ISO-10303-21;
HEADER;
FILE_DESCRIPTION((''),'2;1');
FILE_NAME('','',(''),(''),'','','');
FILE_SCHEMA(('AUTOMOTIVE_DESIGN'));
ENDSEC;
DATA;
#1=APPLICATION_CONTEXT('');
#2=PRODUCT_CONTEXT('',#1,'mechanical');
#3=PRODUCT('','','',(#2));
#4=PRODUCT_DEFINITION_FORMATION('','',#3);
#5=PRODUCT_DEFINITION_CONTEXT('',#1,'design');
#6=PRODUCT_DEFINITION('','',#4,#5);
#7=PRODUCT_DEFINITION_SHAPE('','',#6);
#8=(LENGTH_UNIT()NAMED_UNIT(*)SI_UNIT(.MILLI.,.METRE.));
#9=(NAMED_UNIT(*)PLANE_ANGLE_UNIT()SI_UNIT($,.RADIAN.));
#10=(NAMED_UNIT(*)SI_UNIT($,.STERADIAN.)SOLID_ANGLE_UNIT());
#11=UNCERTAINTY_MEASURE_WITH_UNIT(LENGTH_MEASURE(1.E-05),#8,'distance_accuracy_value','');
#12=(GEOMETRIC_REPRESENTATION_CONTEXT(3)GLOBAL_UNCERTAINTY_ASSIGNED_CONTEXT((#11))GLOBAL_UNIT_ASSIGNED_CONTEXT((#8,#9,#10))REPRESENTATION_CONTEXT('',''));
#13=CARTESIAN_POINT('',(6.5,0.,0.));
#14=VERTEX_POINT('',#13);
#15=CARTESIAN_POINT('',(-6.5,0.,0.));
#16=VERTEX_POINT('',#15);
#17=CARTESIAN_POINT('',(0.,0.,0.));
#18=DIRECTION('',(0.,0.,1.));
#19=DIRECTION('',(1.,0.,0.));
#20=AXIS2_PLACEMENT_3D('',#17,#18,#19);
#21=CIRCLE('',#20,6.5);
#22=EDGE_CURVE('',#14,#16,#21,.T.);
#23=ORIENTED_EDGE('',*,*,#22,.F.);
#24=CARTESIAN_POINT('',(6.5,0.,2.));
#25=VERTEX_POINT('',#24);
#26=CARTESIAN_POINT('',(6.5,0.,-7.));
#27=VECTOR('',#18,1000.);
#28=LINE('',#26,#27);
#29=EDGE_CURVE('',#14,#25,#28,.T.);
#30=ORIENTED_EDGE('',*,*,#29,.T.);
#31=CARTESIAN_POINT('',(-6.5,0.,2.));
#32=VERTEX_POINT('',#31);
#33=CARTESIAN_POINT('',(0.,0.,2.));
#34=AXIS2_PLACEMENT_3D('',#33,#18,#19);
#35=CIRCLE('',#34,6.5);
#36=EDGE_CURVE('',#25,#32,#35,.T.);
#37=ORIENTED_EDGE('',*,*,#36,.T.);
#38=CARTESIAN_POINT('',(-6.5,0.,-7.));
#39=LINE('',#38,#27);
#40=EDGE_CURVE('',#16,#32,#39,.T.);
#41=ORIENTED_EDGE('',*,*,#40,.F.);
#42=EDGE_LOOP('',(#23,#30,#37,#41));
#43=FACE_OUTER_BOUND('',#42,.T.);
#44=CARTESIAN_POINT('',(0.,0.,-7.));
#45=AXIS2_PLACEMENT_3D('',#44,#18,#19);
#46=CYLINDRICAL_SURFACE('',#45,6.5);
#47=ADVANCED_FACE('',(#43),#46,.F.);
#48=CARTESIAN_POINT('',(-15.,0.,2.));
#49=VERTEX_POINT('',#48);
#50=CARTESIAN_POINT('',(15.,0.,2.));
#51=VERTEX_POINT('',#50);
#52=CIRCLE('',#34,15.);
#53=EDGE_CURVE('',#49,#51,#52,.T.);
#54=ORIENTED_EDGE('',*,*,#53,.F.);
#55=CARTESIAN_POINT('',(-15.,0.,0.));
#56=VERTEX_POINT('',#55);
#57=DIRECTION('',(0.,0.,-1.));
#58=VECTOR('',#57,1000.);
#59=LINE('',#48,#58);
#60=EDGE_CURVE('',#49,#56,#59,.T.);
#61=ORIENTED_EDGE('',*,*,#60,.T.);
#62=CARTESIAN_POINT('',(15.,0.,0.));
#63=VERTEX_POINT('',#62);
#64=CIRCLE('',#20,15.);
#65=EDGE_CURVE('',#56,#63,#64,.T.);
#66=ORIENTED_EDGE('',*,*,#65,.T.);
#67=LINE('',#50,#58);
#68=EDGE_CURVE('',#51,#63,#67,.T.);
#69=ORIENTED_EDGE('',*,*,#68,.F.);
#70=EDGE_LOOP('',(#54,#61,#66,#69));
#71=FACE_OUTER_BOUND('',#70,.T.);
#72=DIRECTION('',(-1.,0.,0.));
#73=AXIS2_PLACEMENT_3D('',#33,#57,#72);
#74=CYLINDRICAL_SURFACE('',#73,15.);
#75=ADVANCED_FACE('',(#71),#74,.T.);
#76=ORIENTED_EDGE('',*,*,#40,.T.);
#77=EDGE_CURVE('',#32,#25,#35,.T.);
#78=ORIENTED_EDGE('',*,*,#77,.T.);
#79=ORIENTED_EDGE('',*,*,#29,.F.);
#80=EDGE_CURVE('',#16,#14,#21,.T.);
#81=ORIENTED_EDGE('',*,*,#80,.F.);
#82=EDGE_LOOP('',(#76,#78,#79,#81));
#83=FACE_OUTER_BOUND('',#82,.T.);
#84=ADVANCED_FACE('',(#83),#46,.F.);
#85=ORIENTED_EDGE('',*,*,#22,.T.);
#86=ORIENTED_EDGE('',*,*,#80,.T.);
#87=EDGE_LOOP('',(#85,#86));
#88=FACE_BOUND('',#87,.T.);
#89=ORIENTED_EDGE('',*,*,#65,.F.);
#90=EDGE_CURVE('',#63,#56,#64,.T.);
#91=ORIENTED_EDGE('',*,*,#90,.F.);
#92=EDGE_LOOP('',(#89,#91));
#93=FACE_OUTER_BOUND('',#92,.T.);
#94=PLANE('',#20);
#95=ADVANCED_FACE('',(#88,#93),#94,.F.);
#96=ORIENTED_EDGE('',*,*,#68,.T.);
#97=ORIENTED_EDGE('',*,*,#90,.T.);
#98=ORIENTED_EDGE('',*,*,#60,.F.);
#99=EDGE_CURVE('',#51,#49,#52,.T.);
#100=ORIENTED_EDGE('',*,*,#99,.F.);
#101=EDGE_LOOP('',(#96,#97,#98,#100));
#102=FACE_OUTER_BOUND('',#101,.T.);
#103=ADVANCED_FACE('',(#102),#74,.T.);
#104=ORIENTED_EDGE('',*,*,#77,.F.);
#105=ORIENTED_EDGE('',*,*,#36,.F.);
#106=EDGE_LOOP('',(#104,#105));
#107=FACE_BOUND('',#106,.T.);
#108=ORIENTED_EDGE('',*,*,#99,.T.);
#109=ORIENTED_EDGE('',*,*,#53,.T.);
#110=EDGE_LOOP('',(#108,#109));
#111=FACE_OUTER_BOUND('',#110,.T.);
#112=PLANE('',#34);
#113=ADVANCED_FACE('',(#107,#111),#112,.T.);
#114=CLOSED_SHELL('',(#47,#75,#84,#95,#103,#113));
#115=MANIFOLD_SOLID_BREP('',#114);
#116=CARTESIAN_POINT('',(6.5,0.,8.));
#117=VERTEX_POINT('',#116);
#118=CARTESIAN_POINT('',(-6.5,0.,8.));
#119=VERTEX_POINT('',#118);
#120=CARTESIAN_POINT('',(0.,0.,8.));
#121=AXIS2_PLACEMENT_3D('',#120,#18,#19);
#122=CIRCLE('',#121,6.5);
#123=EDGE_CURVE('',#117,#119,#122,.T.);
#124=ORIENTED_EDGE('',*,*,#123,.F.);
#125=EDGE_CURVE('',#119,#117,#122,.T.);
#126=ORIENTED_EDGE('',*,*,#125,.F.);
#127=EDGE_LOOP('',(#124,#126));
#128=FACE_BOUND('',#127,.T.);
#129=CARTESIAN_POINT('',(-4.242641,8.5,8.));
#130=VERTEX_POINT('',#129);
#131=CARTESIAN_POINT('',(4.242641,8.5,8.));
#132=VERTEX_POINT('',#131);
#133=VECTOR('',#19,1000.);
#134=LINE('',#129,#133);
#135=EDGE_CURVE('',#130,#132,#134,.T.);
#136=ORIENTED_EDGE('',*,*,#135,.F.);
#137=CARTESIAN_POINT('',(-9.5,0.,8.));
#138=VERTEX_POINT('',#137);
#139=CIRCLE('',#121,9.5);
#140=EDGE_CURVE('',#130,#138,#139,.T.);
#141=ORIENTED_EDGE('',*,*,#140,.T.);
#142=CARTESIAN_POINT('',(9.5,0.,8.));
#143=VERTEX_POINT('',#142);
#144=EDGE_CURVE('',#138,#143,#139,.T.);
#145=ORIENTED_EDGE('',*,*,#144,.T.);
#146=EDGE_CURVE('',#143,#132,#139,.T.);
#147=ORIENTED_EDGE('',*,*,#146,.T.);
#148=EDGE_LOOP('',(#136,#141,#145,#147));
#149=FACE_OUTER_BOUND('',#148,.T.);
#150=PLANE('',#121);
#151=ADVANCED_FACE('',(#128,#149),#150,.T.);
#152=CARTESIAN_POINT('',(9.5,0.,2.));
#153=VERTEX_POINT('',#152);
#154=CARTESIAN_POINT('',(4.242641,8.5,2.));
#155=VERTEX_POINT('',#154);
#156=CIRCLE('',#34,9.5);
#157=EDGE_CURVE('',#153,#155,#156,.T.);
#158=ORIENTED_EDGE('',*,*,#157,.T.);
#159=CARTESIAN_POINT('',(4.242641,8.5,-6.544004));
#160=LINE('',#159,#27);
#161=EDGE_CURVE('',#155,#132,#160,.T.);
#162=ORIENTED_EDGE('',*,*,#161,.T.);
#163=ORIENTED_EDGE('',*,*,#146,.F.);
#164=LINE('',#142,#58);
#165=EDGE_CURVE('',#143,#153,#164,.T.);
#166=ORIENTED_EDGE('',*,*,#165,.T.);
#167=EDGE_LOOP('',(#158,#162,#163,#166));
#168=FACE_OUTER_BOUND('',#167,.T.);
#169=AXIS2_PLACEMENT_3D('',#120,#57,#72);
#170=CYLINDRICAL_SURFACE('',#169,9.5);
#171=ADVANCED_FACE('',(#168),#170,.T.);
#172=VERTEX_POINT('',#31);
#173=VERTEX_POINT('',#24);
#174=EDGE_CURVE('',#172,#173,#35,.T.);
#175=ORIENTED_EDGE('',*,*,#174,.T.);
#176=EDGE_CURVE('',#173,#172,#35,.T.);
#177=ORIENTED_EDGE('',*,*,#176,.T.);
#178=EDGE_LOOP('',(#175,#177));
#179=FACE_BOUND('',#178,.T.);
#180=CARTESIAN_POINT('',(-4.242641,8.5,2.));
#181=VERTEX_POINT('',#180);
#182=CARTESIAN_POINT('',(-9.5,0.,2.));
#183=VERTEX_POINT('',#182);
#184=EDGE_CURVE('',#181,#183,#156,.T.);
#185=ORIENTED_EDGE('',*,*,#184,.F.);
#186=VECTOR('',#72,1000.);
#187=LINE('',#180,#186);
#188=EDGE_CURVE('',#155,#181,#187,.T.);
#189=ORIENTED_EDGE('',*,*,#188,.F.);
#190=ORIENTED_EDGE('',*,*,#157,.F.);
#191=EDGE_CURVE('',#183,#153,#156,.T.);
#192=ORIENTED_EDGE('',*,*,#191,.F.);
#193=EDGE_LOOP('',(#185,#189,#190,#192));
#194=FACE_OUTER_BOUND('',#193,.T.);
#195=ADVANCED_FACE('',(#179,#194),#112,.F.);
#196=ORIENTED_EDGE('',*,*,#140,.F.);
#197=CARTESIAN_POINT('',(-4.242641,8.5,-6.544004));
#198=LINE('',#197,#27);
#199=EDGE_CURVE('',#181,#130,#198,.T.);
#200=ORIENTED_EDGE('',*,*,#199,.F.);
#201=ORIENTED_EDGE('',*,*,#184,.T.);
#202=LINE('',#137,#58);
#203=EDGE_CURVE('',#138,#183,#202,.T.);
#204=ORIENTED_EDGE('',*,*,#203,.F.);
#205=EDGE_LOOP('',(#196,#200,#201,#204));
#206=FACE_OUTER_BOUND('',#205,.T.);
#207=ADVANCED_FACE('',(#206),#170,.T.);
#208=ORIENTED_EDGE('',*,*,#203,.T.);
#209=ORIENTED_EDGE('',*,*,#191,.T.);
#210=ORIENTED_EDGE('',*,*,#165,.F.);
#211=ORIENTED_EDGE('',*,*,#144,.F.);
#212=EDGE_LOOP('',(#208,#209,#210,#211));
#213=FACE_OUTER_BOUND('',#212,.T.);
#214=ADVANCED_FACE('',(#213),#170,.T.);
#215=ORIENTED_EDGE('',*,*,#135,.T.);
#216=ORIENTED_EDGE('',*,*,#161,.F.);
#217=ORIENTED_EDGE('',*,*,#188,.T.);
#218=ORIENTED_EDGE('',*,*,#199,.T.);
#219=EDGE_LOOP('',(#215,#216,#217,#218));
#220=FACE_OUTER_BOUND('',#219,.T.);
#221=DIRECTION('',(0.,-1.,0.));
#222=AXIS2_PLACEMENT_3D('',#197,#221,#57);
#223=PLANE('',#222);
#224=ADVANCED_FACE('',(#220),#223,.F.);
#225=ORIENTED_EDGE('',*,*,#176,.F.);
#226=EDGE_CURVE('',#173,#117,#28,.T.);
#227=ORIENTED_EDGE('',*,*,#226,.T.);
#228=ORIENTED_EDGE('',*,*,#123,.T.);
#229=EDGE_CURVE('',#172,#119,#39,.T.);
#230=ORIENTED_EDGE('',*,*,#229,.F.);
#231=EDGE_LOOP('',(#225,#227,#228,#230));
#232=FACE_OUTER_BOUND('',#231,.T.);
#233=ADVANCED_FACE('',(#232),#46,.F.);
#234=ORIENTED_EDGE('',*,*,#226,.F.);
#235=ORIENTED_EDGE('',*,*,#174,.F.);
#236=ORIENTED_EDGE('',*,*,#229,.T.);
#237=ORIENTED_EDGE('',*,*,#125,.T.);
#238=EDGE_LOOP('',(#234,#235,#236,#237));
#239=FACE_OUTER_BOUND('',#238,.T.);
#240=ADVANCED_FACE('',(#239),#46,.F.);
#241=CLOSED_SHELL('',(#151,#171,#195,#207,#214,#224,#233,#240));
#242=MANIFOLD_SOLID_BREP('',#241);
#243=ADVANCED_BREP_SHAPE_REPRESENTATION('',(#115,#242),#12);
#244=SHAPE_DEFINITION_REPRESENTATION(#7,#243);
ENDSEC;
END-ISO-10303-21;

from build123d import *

# Parameters (mm, degrees)
SKETCH_1_R          = 15
EXTRUDE_1_DEPTH     = 2
SKETCH_2_R          = 9.5
EXTRUDE_2_DEPTH     = 6
SKETCH_3_R          = 6.5
CUT_EXTRUDE_1_DEPTH = 15
CUT_EXTRUDE_2_DEPTH = 6


with BuildPart() as part:
    # 草图1 → 凸台-拉伸1 (new body)
    with BuildSketch(Plane.XY):
        Circle(SKETCH_1_R)
    extrude(amount=EXTRUDE_1_DEPTH)


with BuildPart() as body_2:
    # 草图2 → 凸台-拉伸2 (new body)
    with BuildSketch(Plane.XY.offset(2)):
        Circle(SKETCH_2_R)
    extrude(amount=EXTRUDE_2_DEPTH)


with BuildPart() as cut_extrude_1_tool:
    # 草图3 → 切除-拉伸1 (new body)
    with BuildSketch(Plane.XY.offset(8)):
        Circle(SKETCH_3_R)
    extrude(amount=-CUT_EXTRUDE_1_DEPTH)


with BuildPart() as part_1:
    add(part.part)

    # 切除-拉伸1: cut by cut_extrude_1_tool
    add(cut_extrude_1_tool.part, mode=Mode.SUBTRACT)


with BuildPart() as body_2_1:
    add(body_2.part)

    # 切除-拉伸1: cut by cut_extrude_1_tool
    add(cut_extrude_1_tool.part, mode=Mode.SUBTRACT)

    # 草图4 → 切除-拉伸2 (cut)
    with BuildSketch(Plane.XY.offset(8)):
        with BuildLine():
            Line((-4.242640687, 8.5), (4.242640687, 8.5))
            ThreePointArc((4.242640687, 8.5), (0, 9.5), (-4.242640687, 8.5))
        make_face()
    extrude(amount=-CUT_EXTRUDE_2_DEPTH, mode=Mode.SUBTRACT)


solid = Compound([part_1.part, body_2_1.part])
